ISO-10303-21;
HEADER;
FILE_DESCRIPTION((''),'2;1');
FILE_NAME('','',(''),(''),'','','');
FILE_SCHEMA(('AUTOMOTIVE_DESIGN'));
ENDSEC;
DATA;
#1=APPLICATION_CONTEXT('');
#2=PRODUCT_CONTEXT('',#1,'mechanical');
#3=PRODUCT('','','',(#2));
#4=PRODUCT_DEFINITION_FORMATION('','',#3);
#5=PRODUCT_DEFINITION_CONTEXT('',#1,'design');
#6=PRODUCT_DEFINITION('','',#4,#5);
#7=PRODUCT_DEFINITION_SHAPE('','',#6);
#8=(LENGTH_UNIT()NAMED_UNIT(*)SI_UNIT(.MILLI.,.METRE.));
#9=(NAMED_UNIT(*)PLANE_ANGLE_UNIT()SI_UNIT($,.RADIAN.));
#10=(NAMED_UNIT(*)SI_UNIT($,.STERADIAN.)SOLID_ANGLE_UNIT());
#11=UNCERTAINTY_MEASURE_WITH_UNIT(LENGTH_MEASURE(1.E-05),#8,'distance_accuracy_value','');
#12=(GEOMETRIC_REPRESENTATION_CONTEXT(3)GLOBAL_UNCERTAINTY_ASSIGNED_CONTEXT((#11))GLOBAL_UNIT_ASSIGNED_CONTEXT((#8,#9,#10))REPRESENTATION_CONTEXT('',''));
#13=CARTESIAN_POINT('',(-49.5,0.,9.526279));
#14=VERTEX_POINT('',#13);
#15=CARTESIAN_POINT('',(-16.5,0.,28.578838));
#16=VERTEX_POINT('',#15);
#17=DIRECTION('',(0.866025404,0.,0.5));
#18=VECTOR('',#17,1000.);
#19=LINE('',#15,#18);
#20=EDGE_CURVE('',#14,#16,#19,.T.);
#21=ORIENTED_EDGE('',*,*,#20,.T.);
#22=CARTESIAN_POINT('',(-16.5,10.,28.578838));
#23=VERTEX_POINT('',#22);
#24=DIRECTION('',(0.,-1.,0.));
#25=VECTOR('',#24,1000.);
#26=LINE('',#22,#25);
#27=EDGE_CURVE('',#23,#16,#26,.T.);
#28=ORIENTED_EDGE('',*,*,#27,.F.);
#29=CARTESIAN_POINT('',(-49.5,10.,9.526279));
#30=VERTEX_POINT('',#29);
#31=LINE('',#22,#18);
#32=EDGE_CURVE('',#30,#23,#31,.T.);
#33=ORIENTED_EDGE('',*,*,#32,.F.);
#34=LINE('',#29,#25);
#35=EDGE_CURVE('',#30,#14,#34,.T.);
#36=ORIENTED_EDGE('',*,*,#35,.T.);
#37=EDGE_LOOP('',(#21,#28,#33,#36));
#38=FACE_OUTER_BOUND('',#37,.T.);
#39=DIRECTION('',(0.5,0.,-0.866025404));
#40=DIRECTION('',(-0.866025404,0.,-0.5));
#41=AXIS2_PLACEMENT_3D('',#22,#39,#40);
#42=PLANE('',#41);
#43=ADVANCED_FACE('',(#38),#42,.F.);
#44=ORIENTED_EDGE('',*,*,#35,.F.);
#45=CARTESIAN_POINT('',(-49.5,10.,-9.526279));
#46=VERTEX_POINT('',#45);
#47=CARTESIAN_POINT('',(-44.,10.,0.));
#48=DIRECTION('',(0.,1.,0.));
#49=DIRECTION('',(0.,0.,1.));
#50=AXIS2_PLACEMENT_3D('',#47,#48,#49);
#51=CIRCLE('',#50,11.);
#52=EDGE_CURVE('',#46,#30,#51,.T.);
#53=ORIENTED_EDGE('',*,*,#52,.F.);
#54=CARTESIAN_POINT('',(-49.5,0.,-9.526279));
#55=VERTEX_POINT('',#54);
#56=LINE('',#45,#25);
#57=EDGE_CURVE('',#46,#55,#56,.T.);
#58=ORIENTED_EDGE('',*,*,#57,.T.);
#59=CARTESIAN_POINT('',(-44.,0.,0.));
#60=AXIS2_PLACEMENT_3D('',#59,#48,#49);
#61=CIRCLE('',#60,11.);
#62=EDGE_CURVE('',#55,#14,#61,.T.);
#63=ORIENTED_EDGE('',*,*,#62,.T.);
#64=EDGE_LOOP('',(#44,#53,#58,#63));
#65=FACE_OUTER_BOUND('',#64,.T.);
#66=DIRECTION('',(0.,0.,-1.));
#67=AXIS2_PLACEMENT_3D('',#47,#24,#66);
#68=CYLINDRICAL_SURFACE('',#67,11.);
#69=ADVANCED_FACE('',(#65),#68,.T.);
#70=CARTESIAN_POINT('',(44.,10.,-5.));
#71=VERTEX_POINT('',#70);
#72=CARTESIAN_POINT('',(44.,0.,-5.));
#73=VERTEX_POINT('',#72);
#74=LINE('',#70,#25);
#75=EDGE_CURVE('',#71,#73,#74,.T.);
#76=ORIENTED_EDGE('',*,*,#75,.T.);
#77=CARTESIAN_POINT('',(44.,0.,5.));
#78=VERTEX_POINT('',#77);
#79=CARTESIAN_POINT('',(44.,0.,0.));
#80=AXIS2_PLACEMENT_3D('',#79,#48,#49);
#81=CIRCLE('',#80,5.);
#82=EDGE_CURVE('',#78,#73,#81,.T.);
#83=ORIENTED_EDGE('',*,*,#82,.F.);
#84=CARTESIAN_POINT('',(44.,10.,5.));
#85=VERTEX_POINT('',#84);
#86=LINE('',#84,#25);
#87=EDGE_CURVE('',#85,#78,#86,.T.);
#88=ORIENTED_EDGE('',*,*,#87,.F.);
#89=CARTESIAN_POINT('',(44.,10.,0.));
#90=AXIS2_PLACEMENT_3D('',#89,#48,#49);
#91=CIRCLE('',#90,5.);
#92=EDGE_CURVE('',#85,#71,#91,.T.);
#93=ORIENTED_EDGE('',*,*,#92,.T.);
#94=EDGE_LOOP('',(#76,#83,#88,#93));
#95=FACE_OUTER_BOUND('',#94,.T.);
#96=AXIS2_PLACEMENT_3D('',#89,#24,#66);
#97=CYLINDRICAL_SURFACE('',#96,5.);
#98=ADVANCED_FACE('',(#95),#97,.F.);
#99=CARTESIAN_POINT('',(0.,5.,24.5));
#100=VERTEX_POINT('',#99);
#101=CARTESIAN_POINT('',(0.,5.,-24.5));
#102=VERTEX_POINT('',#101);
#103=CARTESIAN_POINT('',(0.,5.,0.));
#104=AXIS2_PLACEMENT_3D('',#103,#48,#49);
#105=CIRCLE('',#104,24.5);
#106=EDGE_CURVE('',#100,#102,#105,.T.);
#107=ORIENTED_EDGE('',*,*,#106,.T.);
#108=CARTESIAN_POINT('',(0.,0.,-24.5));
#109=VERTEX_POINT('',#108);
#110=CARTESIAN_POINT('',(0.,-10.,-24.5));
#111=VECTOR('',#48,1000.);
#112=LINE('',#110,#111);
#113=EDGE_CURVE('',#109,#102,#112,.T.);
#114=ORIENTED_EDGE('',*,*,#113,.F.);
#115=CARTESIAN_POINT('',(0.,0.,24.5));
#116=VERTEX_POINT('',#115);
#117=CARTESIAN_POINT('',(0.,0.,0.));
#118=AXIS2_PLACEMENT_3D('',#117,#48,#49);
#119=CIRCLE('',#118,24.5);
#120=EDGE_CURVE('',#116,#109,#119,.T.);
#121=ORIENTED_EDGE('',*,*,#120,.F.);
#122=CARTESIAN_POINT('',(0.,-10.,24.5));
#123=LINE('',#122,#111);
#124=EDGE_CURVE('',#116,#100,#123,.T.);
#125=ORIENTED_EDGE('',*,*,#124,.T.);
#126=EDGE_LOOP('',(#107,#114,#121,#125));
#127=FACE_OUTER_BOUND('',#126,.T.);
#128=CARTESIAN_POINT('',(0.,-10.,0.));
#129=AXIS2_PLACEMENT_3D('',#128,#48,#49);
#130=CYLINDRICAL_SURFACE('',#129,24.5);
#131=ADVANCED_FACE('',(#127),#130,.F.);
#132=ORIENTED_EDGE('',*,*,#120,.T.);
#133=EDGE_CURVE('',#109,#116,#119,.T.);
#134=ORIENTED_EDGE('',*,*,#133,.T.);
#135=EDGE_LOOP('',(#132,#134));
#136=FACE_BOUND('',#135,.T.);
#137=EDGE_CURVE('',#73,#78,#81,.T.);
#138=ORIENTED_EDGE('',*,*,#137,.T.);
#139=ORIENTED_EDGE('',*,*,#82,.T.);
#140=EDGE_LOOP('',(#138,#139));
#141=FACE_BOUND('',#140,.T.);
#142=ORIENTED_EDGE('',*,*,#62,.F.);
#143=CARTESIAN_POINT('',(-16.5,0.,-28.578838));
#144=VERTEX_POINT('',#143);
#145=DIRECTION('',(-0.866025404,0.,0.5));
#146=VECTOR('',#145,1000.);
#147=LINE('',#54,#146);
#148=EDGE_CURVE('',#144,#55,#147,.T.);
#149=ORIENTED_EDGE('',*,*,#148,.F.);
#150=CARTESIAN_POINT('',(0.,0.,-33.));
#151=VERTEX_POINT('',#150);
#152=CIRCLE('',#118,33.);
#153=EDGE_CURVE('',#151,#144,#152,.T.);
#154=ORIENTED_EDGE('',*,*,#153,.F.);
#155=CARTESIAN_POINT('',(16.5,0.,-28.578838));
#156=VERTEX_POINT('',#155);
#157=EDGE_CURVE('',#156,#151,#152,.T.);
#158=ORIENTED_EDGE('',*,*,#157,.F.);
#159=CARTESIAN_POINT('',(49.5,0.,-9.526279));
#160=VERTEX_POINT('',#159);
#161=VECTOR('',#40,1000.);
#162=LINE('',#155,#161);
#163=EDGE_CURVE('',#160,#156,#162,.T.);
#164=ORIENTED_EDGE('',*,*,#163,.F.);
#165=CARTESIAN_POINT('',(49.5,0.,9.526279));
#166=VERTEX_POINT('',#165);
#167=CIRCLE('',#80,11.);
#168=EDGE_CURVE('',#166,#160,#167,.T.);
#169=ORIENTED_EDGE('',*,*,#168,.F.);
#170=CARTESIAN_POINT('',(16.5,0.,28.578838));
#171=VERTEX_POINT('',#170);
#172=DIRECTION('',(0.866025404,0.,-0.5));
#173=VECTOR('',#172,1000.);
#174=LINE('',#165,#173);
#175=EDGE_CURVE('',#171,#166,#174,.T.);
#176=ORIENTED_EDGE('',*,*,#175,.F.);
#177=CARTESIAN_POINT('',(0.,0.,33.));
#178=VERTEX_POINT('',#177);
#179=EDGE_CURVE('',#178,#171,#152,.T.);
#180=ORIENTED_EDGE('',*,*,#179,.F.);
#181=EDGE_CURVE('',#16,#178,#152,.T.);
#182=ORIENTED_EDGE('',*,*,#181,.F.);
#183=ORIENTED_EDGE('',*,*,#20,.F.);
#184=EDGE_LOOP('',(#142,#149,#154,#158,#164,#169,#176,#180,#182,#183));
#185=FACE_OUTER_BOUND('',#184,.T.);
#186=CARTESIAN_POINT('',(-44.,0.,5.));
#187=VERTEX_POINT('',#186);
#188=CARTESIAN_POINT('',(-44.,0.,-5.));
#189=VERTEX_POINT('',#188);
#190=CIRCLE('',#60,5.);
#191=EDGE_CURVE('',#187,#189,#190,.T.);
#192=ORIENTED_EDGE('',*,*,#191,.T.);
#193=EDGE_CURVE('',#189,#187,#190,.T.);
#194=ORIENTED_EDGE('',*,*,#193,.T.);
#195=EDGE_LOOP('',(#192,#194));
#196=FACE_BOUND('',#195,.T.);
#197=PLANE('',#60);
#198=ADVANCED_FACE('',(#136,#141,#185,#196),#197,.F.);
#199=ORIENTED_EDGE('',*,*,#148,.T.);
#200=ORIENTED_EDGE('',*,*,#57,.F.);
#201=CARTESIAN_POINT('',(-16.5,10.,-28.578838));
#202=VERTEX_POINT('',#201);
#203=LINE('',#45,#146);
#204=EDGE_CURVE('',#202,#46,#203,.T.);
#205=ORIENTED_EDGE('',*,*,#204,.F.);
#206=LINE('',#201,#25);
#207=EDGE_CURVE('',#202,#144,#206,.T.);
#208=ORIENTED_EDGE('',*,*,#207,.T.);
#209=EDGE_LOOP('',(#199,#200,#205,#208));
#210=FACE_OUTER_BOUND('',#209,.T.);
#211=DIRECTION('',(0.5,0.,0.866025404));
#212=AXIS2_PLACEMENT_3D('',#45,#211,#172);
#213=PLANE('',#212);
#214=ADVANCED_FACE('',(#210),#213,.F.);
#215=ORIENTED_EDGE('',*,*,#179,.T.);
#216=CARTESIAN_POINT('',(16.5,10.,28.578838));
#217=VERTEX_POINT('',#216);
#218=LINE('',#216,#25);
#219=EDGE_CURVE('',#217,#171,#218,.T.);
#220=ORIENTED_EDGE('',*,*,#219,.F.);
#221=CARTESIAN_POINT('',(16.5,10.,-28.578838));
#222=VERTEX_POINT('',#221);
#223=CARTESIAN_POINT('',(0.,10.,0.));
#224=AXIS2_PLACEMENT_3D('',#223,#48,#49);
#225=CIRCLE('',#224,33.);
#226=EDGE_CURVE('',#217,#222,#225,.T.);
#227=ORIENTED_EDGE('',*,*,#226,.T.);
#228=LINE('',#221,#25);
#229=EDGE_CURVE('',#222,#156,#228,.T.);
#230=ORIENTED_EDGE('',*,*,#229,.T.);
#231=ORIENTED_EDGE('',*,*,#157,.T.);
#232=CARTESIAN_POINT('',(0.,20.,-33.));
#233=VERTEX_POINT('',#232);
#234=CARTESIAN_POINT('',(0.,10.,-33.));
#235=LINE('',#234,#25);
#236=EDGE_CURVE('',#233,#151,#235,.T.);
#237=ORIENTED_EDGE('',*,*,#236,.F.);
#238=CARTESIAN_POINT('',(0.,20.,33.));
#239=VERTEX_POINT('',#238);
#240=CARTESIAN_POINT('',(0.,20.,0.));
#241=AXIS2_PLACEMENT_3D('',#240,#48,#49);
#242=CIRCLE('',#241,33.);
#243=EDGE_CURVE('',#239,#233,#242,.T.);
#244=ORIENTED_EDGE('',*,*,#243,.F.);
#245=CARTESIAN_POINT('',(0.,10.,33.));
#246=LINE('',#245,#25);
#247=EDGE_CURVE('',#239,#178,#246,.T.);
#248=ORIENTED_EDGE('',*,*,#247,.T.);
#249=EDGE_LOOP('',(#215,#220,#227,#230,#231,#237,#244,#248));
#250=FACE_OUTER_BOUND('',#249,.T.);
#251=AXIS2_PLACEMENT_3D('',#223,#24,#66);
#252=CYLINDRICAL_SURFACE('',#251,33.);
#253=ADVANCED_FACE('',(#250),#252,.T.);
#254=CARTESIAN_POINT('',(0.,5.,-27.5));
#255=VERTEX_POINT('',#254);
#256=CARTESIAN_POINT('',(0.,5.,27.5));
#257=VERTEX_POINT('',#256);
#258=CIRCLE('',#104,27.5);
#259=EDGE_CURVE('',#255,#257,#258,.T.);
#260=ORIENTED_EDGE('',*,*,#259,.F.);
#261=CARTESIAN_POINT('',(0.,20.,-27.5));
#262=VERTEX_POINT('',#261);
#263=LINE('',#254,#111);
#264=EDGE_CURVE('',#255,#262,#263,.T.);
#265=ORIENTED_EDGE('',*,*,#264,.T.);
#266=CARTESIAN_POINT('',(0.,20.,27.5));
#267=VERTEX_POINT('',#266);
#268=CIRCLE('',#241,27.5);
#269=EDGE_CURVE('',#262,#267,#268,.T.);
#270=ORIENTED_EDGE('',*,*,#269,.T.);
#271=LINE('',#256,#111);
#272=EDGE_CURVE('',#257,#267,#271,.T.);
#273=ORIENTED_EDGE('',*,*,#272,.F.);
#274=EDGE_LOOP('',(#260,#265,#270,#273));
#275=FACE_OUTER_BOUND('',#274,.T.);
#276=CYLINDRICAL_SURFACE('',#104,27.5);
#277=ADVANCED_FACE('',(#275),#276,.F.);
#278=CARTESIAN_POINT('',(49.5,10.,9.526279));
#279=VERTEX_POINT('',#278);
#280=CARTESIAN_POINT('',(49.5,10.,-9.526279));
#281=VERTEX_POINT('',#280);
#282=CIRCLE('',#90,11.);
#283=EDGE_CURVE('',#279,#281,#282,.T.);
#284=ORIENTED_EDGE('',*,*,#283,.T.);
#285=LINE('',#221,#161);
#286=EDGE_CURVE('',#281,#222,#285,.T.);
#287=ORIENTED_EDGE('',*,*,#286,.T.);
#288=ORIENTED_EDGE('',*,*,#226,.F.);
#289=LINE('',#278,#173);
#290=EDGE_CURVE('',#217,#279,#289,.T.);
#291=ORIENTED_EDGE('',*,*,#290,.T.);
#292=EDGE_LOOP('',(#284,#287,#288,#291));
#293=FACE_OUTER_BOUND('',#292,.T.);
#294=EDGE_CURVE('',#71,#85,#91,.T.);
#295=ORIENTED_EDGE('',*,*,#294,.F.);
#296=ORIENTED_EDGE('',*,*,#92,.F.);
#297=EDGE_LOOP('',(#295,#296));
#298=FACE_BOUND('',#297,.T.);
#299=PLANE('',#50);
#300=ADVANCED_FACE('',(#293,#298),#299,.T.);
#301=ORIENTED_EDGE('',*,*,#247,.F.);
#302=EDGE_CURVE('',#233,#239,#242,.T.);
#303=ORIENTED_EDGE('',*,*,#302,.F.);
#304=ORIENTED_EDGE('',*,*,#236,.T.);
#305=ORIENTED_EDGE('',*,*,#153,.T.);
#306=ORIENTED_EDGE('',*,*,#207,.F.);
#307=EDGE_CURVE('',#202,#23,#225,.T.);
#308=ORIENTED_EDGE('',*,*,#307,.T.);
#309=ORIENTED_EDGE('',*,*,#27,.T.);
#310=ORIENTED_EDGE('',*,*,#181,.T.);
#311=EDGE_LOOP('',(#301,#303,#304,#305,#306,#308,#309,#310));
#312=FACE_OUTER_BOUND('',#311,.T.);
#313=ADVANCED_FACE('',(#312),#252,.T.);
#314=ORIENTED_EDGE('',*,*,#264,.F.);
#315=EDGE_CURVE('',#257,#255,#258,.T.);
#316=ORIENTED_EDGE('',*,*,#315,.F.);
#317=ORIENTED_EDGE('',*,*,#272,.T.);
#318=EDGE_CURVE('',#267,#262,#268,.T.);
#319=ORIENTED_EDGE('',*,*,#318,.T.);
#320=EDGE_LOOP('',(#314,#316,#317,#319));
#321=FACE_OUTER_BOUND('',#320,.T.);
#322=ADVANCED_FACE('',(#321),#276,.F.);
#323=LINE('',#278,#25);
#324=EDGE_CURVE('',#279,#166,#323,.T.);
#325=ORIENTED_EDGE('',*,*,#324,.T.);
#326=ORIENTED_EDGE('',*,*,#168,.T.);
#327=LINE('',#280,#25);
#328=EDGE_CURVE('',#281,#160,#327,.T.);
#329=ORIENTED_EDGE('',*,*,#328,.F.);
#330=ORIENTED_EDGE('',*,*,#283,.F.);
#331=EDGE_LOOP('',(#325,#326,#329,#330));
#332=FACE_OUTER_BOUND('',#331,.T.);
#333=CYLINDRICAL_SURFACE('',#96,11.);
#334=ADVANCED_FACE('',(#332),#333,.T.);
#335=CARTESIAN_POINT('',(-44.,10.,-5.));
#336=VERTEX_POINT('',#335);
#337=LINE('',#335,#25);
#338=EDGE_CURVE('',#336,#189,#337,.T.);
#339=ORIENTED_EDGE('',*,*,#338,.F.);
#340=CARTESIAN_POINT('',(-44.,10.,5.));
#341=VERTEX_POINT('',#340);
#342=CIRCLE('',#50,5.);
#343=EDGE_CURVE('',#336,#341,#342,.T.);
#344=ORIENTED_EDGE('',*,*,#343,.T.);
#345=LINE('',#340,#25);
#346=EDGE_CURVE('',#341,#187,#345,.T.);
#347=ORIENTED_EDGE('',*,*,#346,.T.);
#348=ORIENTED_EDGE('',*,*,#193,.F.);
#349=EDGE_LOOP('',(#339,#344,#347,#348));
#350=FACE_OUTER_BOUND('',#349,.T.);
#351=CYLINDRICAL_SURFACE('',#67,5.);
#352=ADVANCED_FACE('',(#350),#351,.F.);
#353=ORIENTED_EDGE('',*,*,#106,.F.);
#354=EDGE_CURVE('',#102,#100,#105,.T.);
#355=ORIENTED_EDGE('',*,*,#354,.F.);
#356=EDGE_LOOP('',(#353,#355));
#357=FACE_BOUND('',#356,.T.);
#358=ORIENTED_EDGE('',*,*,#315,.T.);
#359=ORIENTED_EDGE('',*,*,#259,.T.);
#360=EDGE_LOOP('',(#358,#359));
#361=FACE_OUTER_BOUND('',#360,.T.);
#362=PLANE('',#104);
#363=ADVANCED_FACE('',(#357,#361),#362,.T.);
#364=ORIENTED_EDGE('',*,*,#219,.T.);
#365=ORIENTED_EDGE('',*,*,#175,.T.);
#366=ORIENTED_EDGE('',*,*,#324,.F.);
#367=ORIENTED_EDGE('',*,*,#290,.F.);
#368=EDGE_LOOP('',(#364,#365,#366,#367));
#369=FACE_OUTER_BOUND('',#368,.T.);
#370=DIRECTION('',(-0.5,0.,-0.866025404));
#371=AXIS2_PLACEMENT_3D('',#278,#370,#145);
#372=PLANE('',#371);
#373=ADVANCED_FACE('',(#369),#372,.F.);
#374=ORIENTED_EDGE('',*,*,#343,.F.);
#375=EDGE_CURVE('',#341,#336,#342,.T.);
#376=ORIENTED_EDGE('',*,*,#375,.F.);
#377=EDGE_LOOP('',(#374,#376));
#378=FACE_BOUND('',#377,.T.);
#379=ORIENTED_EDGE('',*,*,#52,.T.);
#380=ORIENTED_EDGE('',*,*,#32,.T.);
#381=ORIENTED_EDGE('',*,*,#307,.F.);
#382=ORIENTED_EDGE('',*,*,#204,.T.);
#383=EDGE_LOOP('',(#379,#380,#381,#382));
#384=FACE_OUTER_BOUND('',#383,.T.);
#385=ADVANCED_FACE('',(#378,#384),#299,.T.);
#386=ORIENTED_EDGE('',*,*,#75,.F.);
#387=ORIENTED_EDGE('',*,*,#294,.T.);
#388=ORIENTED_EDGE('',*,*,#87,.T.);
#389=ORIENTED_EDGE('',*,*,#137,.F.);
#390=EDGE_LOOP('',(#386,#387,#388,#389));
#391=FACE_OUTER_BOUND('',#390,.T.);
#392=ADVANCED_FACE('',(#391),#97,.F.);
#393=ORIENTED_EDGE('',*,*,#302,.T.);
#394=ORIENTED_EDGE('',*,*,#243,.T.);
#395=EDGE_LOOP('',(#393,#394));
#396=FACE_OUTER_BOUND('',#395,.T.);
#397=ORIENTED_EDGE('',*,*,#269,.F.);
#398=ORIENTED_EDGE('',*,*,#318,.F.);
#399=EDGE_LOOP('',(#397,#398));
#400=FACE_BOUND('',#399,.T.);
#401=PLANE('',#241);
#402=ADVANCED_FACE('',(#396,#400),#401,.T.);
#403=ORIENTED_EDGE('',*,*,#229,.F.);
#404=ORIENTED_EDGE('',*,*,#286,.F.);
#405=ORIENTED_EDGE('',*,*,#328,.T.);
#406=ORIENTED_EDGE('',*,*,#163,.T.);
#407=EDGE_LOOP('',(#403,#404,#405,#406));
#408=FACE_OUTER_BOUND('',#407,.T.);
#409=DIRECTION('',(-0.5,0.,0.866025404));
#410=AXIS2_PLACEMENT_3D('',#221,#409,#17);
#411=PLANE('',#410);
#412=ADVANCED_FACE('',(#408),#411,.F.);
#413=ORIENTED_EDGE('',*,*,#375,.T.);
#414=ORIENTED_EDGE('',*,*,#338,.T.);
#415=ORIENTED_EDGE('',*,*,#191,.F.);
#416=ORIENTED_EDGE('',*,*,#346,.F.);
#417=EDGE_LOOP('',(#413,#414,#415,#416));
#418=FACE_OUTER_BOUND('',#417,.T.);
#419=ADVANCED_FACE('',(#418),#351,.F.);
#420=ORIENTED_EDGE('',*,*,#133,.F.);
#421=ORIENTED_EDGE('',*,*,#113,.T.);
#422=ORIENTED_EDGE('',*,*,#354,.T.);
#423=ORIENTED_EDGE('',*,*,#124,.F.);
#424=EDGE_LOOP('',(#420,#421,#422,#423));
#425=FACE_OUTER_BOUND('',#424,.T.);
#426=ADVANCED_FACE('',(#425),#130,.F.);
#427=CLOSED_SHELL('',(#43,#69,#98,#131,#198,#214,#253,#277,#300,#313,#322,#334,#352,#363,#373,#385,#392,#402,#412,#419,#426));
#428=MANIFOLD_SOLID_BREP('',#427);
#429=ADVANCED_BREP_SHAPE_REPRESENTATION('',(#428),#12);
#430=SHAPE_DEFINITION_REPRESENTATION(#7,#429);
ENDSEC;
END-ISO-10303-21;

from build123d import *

# Parameters (mm, degrees)
SKETCH_1_R          = 5
EXTRUDE_1_DEPTH     = 10
SKETCH_2_R          = 33
EXTRUDE_2_DEPTH     = 10
SKETCH_3_R          = 27.5
CUT_EXTRUDE_1_DEPTH = 15
SKETCH_4_R          = 24.5
CUT_EXTRUDE_2_DEPTH = 15


with BuildPart() as part:
    # 草图1 → 凸台-拉伸1 (new body)
    with BuildSketch(Plane(origin=(0, 0, 0), x_dir=(1, 0, 0), z_dir=(0, 1, 0))):
        with BuildLine():
            Line((-49.5, 9.526279442), (-16.5, 28.578838325))
            ThreePointArc((-16.5, 28.578838325), (0, 33), (16.5, 28.578838325))
            Line((16.5, 28.578838325), (49.5, 9.526279442))
            ThreePointArc((49.5, 9.526279442), (55, 0), (49.5, -9.526279442))
            Line((49.5, -9.526279442), (16.5, -28.578838325))
            ThreePointArc((16.5, -28.578838325), (0, -33), (-16.5, -28.578838325))
            Line((-16.5, -28.578838325), (-49.5, -9.526279442))
            ThreePointArc((-49.5, -9.526279442), (-55, 0), (-49.5, 9.526279442))
        make_face()
        with Locations(Location((-44, 0, 0), (0, 0, 270))):
            Circle(SKETCH_1_R, mode=Mode.SUBTRACT)
        with Locations(Location((44, 0, 0), (0, 0, 270))):
            Circle(SKETCH_1_R, mode=Mode.SUBTRACT)
    extrude(amount=EXTRUDE_1_DEPTH)

    # 草图2 → 凸台-拉伸2 (add)
    with BuildSketch(Plane(origin=(0, 10, 0), x_dir=(1, 0, 0), z_dir=(0, 1, 0))):
        with Locations(Location((0, 0, 0), (0, 0, 120))):
            Circle(SKETCH_2_R)
    extrude(amount=EXTRUDE_2_DEPTH)

    # 草图3 → 切除-拉伸1 (cut)
    with BuildSketch(Plane(origin=(0, 20, 0), x_dir=(1, 0, 0), z_dir=(0, 1, 0))):
        with Locations(Location((0, 0, 0), (0, 0, 270))):
            Circle(SKETCH_3_R)
    extrude(amount=-CUT_EXTRUDE_1_DEPTH, mode=Mode.SUBTRACT)

    # 草图4 → 切除-拉伸2 (cut)
    with BuildSketch(Plane(origin=(0, 5, 0), x_dir=(1, 0, 0), z_dir=(0, 1, 0))):
        with Locations(Location((0, 0, 0), (0, 0, 270))):
            Circle(SKETCH_4_R)
    extrude(amount=-CUT_EXTRUDE_2_DEPTH, mode=Mode.SUBTRACT)


solid = part.part
